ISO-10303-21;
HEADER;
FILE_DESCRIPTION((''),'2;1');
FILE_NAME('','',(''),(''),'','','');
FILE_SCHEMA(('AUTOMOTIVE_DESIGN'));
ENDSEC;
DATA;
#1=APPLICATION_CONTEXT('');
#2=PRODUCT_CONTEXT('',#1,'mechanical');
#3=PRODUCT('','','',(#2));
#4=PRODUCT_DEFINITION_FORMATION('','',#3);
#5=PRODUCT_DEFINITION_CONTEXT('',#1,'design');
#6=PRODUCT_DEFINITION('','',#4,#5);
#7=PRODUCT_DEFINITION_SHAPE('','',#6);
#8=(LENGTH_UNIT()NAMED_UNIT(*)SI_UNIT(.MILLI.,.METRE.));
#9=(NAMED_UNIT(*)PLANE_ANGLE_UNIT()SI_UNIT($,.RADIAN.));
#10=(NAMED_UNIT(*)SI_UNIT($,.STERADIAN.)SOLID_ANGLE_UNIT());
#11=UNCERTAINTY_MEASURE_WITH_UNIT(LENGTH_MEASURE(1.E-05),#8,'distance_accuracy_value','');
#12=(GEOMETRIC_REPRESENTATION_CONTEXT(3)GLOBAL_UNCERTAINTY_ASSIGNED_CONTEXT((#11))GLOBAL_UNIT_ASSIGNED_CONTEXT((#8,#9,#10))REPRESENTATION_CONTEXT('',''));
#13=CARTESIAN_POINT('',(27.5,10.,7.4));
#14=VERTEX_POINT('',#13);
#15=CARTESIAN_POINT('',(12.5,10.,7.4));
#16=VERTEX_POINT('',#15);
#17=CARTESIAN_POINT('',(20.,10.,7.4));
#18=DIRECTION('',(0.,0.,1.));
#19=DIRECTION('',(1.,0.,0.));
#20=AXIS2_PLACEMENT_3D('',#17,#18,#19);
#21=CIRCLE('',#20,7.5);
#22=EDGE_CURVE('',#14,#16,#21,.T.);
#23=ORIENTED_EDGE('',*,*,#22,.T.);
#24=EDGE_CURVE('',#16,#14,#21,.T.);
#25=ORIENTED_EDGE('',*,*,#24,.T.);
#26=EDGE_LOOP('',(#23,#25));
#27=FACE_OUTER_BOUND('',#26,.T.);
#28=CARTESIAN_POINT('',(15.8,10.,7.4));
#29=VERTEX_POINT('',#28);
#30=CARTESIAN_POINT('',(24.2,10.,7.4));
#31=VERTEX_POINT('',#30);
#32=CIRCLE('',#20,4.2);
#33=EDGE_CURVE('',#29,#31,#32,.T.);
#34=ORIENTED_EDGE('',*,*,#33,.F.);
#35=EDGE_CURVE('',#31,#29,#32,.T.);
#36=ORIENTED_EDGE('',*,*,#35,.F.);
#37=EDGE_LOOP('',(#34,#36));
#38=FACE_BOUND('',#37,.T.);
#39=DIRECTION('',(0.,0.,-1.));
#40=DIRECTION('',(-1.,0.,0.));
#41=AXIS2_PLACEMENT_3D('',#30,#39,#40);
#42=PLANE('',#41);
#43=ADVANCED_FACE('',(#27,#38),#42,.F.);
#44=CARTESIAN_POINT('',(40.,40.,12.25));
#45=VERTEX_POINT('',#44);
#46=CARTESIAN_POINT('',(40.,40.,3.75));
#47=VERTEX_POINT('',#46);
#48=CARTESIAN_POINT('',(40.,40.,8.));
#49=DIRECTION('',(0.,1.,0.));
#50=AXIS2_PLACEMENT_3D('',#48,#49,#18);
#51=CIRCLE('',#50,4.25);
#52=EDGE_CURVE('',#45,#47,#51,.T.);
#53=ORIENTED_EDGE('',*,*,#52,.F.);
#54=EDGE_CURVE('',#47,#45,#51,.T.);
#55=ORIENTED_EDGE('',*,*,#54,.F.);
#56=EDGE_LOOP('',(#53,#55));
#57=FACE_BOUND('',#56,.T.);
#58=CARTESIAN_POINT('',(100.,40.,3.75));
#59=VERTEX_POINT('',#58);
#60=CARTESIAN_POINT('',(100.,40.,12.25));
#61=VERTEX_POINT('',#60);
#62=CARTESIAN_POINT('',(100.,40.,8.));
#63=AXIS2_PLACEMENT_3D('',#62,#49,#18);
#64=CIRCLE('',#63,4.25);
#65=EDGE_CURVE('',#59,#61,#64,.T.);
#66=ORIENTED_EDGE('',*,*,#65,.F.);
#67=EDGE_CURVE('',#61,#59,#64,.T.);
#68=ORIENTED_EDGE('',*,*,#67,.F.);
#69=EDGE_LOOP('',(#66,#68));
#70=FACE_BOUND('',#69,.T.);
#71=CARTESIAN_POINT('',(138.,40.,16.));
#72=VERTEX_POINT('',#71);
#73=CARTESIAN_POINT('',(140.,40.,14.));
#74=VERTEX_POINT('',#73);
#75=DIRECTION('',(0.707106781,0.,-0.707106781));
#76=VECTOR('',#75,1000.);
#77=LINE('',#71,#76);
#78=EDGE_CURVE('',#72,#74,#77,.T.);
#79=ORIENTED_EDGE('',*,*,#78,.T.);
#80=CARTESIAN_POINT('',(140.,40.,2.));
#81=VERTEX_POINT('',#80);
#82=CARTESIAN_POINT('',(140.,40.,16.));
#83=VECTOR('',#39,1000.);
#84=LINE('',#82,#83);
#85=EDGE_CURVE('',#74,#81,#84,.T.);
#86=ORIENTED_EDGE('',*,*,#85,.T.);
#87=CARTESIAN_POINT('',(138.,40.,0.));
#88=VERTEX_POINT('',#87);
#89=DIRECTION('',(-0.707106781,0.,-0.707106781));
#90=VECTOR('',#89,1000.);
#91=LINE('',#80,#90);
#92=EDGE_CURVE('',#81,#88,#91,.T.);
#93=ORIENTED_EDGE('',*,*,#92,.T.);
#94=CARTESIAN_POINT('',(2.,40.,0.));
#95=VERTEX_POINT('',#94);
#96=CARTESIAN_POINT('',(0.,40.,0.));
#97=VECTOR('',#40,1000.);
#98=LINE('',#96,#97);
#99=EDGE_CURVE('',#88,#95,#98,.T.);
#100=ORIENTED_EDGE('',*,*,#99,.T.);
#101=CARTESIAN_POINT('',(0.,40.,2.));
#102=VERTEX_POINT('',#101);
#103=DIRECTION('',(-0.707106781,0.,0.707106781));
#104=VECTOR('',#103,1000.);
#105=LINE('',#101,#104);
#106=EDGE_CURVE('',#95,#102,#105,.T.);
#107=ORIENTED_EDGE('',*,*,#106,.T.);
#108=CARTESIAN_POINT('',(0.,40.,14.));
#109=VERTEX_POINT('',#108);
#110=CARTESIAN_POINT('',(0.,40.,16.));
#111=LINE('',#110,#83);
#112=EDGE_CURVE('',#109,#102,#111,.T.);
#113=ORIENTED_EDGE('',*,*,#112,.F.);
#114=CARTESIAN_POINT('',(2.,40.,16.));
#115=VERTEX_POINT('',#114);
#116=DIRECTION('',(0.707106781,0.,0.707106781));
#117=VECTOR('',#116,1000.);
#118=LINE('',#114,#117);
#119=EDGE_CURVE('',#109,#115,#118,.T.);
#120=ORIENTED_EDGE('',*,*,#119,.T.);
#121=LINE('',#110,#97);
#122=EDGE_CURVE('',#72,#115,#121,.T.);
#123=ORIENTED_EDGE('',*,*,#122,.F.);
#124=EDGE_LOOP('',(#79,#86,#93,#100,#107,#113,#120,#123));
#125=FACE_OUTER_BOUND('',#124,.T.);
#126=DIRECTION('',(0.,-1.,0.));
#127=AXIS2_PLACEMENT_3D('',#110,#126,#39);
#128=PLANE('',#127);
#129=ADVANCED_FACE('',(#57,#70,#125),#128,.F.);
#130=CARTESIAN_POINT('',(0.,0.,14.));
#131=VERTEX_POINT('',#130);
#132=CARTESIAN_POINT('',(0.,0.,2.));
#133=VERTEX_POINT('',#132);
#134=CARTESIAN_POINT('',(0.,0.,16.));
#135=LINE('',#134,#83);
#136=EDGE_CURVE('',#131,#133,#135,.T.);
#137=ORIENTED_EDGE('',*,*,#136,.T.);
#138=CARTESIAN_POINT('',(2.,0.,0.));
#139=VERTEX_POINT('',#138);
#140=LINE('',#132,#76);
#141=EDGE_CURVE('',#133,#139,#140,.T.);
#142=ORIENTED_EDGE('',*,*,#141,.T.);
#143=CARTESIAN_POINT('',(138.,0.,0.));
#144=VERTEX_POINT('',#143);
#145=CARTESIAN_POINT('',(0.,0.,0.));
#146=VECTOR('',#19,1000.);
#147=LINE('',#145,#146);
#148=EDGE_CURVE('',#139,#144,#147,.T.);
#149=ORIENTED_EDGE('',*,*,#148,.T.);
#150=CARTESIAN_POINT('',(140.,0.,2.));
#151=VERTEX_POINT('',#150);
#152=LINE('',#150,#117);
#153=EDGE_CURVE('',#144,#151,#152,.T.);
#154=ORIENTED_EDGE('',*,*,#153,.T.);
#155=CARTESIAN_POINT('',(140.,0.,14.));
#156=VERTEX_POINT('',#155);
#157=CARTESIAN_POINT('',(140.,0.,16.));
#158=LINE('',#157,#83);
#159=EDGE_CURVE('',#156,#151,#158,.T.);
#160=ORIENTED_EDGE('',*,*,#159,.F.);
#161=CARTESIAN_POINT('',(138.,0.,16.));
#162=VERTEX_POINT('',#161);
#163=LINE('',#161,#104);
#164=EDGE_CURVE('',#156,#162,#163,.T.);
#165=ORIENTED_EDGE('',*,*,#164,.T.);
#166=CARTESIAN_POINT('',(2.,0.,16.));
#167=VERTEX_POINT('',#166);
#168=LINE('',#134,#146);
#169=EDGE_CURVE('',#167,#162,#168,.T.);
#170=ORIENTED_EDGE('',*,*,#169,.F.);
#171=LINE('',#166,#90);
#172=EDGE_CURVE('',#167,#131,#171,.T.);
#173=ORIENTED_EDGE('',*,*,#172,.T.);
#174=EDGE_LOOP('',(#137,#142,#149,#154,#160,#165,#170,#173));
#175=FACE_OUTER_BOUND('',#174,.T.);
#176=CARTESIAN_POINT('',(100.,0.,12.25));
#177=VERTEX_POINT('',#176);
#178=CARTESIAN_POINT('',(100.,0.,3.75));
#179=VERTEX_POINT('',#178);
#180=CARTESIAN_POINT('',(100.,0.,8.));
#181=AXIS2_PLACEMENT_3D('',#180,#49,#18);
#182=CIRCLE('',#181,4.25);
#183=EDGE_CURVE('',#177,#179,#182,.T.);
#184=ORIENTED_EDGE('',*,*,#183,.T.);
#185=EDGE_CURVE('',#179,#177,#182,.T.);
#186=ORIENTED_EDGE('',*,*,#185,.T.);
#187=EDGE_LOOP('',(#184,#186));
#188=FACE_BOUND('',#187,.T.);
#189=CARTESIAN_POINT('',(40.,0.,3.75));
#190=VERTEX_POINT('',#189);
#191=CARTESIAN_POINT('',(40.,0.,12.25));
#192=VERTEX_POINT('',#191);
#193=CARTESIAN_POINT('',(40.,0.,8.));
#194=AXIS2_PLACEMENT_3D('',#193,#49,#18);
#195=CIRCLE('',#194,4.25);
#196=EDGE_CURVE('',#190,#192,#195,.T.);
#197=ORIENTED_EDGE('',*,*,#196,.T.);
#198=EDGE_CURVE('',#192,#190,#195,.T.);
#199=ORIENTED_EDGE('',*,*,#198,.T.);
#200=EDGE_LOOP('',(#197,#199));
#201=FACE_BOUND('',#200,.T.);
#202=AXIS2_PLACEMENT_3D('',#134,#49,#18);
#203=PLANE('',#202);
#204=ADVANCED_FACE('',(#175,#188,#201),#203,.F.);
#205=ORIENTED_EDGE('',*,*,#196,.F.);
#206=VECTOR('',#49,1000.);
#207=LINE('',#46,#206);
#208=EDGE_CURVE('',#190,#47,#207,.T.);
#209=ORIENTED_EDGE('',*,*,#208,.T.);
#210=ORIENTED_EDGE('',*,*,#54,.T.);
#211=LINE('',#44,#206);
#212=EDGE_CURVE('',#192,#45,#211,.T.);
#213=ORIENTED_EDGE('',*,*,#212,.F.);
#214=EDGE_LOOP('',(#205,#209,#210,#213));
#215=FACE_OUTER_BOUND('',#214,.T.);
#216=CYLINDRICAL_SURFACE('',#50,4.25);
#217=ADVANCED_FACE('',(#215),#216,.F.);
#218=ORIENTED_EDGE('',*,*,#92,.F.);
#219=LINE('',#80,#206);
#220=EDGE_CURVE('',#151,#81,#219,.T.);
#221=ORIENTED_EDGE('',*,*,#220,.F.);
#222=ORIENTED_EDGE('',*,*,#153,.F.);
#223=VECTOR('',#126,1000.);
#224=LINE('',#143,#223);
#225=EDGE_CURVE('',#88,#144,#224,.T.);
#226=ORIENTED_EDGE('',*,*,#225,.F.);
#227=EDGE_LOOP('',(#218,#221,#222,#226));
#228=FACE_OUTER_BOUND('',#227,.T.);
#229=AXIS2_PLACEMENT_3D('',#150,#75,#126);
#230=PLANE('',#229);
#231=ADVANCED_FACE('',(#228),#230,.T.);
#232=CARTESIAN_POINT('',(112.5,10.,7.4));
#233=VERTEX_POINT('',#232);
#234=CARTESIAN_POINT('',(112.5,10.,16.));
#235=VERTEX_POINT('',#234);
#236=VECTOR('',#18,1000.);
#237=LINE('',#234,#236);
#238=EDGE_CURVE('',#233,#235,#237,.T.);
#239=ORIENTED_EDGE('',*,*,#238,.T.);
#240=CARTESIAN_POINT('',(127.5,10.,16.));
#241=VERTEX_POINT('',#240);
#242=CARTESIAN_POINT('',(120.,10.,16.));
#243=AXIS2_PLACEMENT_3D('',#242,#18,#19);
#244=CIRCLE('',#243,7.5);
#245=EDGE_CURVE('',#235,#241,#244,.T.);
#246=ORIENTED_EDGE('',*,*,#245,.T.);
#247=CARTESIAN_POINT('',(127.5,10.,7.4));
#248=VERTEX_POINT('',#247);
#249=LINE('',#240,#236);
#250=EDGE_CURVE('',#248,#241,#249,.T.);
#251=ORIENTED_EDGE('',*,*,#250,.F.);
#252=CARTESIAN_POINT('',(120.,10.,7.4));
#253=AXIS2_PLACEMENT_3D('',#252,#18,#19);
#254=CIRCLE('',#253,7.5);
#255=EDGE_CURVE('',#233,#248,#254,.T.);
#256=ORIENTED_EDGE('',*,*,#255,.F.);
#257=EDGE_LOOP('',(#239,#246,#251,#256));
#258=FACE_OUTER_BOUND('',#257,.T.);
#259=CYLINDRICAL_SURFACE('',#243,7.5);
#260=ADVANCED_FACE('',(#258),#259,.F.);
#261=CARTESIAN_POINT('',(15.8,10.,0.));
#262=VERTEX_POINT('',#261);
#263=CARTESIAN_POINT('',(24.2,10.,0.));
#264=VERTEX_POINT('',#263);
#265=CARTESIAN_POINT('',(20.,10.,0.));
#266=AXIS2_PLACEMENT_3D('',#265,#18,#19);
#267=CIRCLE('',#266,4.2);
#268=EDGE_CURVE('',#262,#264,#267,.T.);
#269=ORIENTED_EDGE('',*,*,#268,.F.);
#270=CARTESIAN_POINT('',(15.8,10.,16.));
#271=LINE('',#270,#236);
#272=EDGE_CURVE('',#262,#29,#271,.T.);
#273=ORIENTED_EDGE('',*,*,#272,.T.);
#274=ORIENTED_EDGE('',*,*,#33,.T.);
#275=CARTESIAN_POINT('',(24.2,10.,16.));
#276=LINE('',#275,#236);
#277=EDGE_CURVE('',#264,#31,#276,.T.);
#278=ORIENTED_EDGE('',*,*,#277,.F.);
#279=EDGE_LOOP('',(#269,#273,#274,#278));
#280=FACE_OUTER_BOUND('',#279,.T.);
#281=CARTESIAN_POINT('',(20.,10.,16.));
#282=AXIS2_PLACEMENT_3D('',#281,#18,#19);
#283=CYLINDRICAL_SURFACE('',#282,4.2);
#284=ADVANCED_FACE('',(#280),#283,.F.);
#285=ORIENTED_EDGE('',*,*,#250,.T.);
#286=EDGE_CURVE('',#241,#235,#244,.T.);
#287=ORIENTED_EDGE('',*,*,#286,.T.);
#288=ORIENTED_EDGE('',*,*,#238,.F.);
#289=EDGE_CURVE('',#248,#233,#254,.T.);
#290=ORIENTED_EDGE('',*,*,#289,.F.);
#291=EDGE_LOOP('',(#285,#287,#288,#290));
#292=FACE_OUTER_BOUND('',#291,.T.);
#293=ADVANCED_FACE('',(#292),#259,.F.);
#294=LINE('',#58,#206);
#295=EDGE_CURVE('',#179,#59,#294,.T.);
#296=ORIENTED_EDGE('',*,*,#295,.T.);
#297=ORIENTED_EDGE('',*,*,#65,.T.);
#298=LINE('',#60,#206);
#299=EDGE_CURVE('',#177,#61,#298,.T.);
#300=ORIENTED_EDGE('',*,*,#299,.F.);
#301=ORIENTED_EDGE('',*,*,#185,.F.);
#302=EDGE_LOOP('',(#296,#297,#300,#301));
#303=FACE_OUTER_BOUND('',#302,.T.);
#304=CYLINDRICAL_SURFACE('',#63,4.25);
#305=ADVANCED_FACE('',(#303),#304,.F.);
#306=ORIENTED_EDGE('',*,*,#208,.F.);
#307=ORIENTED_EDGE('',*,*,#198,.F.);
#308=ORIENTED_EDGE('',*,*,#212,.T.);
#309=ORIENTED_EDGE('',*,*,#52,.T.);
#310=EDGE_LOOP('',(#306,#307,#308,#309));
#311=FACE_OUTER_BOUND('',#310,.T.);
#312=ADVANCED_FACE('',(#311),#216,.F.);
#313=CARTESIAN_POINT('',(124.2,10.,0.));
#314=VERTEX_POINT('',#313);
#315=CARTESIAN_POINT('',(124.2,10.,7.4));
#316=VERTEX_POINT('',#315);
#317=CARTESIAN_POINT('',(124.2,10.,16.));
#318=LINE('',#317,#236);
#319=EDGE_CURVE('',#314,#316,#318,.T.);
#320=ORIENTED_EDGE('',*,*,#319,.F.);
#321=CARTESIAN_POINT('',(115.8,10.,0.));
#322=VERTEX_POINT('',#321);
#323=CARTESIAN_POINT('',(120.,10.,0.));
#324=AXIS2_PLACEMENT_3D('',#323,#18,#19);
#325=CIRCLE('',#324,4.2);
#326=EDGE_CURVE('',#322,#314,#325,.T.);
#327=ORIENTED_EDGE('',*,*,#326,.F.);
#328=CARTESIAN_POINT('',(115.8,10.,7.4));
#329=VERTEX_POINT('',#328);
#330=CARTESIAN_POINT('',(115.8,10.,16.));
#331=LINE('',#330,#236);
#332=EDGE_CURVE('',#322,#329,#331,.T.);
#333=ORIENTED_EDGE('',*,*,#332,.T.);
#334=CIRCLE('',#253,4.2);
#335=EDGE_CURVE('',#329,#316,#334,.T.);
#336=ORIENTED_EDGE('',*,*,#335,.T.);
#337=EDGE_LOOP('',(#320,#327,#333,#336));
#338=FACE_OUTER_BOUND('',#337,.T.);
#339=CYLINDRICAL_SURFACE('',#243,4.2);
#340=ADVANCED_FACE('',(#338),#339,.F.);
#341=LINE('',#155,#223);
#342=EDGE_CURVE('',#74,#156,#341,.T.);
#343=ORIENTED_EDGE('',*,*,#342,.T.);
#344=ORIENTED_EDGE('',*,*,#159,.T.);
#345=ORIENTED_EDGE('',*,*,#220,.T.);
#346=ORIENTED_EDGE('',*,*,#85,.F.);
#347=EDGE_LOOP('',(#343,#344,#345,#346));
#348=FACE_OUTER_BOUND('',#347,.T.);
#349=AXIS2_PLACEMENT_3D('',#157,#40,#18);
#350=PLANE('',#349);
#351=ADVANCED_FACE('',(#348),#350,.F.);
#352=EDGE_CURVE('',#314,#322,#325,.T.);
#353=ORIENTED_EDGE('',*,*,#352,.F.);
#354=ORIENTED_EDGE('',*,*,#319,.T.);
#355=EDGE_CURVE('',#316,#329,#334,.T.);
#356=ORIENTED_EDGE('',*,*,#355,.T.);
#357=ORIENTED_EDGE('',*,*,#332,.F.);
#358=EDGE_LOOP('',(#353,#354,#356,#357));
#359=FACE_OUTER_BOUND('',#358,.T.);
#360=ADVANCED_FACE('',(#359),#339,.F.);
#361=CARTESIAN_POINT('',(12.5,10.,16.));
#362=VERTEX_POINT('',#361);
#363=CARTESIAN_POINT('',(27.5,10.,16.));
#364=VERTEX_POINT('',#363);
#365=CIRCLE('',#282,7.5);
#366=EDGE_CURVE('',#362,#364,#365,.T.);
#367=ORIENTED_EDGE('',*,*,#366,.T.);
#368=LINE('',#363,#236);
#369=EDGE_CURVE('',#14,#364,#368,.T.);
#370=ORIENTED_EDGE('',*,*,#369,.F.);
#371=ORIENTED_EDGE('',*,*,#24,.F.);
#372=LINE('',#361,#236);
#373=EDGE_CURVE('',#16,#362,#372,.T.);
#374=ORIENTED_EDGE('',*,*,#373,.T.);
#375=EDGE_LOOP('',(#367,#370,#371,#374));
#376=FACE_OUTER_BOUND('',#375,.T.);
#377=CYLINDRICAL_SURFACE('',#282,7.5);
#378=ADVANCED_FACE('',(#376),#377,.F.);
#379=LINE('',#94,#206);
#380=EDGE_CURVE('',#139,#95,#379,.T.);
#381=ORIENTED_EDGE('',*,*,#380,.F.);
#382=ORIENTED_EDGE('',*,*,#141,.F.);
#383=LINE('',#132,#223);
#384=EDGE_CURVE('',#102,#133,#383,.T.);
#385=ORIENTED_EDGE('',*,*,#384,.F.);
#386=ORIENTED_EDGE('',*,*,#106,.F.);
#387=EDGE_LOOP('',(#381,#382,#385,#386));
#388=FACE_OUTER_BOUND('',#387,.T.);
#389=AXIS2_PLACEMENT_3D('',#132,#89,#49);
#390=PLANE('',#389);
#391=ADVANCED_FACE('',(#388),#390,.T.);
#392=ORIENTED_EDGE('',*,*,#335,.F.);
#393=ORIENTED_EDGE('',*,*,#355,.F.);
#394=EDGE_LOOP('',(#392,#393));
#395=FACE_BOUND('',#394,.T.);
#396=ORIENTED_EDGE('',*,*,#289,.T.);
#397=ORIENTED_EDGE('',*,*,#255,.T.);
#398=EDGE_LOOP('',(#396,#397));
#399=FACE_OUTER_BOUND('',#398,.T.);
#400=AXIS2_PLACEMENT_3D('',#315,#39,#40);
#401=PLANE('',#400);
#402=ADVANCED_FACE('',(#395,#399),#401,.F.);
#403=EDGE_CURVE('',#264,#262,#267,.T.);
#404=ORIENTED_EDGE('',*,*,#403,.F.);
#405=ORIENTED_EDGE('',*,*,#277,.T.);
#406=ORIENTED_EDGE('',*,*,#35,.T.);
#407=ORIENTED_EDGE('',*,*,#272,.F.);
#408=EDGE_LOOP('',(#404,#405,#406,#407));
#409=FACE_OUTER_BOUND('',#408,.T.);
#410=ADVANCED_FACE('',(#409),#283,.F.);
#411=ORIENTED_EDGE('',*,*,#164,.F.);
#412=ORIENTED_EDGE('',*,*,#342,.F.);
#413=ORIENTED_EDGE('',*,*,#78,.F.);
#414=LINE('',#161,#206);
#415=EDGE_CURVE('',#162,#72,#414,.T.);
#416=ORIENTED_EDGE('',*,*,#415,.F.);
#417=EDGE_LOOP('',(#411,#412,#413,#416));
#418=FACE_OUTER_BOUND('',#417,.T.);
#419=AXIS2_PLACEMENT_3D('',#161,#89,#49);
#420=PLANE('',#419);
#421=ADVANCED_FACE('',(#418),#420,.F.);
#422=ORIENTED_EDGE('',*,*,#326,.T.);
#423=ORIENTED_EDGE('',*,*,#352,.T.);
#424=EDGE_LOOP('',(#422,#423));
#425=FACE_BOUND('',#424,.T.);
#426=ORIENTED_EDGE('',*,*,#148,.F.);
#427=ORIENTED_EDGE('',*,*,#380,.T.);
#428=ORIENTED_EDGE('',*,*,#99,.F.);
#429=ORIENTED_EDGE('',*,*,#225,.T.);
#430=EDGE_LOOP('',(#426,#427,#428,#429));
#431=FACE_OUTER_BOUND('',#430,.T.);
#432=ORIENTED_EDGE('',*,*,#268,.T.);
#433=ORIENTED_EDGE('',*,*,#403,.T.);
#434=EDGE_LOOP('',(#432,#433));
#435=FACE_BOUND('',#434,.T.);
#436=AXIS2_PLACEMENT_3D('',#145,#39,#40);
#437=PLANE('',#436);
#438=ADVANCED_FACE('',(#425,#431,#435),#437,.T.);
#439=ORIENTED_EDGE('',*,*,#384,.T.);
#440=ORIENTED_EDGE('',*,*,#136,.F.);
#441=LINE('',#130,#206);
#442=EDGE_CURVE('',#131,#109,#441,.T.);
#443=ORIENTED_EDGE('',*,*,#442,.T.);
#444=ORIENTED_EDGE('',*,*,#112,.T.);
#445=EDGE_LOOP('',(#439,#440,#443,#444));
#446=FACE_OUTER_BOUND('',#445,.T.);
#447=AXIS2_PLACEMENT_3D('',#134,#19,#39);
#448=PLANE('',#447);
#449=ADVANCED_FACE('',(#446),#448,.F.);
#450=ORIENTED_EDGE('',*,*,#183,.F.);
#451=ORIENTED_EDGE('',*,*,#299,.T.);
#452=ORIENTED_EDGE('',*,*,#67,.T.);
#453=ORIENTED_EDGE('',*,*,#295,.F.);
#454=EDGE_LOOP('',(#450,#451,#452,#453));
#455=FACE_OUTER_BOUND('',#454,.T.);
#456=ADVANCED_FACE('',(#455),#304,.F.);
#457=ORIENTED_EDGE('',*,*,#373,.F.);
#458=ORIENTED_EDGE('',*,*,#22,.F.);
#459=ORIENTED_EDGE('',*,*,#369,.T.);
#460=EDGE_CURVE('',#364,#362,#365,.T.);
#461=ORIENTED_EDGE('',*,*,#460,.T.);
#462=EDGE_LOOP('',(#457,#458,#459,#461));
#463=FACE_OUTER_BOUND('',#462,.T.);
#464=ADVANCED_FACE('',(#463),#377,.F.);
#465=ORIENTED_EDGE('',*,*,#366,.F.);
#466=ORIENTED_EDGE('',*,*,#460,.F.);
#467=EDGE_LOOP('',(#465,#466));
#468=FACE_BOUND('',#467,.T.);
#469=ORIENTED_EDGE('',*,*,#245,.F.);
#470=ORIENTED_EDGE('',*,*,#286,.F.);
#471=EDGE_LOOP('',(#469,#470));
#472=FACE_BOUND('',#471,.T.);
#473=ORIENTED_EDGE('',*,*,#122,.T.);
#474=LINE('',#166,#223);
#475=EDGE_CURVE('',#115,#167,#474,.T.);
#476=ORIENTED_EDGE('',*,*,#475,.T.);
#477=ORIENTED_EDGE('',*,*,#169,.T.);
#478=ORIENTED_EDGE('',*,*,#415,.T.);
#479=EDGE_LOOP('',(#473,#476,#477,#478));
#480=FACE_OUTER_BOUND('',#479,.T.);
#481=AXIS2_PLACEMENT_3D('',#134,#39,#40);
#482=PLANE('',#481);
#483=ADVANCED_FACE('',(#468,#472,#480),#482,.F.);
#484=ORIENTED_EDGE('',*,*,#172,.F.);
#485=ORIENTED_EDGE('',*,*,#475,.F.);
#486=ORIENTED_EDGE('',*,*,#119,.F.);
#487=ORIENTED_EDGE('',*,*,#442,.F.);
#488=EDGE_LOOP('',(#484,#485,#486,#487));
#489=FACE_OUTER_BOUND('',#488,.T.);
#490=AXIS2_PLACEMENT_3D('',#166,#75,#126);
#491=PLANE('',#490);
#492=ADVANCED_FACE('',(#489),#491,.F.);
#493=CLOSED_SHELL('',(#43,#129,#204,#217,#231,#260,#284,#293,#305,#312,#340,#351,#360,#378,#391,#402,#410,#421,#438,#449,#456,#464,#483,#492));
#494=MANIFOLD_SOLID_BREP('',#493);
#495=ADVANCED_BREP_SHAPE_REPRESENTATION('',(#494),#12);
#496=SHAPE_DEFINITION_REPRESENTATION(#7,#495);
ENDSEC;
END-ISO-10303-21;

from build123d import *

# Parameters (mm, degrees)
SKETCH_1_W                   = 140
SKETCH_1_H                   = 40
EXTRUDE_1_DEPTH              = 16
HOLE_WIZARD_M10_1_D          = 8.5
HOLE_WIZARD_M8_1_D           = 8.4
HOLE_WIZARD_M8_1_CBORE_D     = 15
HOLE_WIZARD_M8_1_CBORE_DEPTH = 8.6
CHAMFER_1_SIZE               = 2


with BuildPart() as part:
    # 草图1 → 凸台-拉伸1 (new body)
    with BuildSketch(Plane.XY):
        with Locations((70, 20)):
            Rectangle(SKETCH_1_W, SKETCH_1_H)
    extrude(amount=EXTRUDE_1_DEPTH)

    # M10 螺纹孔1 (through all)
    with Locations(Plane(origin=(0, 40, 0), x_dir=(1, 0, 0), z_dir=(0, 1, 0))):
        with Locations((40, -8), (100, -8)):
            Hole(HOLE_WIZARD_M10_1_D / 2)

    # M8 六角凹头螺钉的柱形沉头孔1 (through all)
    with Locations(Plane.XY.offset(16)):
        with Locations((20, 10), (120, 10)):
            CounterBoreHole(HOLE_WIZARD_M8_1_D / 2, HOLE_WIZARD_M8_1_CBORE_D / 2, HOLE_WIZARD_M8_1_CBORE_DEPTH)

    # 倒角1
    chamfer_1_edges = [part.edges().sort_by_distance(p)[0] for p in [
        (140, 20, 16),
        (0, 20, 16),
        (140, 20, 0),
        (0, 20, 0),
    ]]
    chamfer(chamfer_1_edges, length=CHAMFER_1_SIZE)


solid = part.part
